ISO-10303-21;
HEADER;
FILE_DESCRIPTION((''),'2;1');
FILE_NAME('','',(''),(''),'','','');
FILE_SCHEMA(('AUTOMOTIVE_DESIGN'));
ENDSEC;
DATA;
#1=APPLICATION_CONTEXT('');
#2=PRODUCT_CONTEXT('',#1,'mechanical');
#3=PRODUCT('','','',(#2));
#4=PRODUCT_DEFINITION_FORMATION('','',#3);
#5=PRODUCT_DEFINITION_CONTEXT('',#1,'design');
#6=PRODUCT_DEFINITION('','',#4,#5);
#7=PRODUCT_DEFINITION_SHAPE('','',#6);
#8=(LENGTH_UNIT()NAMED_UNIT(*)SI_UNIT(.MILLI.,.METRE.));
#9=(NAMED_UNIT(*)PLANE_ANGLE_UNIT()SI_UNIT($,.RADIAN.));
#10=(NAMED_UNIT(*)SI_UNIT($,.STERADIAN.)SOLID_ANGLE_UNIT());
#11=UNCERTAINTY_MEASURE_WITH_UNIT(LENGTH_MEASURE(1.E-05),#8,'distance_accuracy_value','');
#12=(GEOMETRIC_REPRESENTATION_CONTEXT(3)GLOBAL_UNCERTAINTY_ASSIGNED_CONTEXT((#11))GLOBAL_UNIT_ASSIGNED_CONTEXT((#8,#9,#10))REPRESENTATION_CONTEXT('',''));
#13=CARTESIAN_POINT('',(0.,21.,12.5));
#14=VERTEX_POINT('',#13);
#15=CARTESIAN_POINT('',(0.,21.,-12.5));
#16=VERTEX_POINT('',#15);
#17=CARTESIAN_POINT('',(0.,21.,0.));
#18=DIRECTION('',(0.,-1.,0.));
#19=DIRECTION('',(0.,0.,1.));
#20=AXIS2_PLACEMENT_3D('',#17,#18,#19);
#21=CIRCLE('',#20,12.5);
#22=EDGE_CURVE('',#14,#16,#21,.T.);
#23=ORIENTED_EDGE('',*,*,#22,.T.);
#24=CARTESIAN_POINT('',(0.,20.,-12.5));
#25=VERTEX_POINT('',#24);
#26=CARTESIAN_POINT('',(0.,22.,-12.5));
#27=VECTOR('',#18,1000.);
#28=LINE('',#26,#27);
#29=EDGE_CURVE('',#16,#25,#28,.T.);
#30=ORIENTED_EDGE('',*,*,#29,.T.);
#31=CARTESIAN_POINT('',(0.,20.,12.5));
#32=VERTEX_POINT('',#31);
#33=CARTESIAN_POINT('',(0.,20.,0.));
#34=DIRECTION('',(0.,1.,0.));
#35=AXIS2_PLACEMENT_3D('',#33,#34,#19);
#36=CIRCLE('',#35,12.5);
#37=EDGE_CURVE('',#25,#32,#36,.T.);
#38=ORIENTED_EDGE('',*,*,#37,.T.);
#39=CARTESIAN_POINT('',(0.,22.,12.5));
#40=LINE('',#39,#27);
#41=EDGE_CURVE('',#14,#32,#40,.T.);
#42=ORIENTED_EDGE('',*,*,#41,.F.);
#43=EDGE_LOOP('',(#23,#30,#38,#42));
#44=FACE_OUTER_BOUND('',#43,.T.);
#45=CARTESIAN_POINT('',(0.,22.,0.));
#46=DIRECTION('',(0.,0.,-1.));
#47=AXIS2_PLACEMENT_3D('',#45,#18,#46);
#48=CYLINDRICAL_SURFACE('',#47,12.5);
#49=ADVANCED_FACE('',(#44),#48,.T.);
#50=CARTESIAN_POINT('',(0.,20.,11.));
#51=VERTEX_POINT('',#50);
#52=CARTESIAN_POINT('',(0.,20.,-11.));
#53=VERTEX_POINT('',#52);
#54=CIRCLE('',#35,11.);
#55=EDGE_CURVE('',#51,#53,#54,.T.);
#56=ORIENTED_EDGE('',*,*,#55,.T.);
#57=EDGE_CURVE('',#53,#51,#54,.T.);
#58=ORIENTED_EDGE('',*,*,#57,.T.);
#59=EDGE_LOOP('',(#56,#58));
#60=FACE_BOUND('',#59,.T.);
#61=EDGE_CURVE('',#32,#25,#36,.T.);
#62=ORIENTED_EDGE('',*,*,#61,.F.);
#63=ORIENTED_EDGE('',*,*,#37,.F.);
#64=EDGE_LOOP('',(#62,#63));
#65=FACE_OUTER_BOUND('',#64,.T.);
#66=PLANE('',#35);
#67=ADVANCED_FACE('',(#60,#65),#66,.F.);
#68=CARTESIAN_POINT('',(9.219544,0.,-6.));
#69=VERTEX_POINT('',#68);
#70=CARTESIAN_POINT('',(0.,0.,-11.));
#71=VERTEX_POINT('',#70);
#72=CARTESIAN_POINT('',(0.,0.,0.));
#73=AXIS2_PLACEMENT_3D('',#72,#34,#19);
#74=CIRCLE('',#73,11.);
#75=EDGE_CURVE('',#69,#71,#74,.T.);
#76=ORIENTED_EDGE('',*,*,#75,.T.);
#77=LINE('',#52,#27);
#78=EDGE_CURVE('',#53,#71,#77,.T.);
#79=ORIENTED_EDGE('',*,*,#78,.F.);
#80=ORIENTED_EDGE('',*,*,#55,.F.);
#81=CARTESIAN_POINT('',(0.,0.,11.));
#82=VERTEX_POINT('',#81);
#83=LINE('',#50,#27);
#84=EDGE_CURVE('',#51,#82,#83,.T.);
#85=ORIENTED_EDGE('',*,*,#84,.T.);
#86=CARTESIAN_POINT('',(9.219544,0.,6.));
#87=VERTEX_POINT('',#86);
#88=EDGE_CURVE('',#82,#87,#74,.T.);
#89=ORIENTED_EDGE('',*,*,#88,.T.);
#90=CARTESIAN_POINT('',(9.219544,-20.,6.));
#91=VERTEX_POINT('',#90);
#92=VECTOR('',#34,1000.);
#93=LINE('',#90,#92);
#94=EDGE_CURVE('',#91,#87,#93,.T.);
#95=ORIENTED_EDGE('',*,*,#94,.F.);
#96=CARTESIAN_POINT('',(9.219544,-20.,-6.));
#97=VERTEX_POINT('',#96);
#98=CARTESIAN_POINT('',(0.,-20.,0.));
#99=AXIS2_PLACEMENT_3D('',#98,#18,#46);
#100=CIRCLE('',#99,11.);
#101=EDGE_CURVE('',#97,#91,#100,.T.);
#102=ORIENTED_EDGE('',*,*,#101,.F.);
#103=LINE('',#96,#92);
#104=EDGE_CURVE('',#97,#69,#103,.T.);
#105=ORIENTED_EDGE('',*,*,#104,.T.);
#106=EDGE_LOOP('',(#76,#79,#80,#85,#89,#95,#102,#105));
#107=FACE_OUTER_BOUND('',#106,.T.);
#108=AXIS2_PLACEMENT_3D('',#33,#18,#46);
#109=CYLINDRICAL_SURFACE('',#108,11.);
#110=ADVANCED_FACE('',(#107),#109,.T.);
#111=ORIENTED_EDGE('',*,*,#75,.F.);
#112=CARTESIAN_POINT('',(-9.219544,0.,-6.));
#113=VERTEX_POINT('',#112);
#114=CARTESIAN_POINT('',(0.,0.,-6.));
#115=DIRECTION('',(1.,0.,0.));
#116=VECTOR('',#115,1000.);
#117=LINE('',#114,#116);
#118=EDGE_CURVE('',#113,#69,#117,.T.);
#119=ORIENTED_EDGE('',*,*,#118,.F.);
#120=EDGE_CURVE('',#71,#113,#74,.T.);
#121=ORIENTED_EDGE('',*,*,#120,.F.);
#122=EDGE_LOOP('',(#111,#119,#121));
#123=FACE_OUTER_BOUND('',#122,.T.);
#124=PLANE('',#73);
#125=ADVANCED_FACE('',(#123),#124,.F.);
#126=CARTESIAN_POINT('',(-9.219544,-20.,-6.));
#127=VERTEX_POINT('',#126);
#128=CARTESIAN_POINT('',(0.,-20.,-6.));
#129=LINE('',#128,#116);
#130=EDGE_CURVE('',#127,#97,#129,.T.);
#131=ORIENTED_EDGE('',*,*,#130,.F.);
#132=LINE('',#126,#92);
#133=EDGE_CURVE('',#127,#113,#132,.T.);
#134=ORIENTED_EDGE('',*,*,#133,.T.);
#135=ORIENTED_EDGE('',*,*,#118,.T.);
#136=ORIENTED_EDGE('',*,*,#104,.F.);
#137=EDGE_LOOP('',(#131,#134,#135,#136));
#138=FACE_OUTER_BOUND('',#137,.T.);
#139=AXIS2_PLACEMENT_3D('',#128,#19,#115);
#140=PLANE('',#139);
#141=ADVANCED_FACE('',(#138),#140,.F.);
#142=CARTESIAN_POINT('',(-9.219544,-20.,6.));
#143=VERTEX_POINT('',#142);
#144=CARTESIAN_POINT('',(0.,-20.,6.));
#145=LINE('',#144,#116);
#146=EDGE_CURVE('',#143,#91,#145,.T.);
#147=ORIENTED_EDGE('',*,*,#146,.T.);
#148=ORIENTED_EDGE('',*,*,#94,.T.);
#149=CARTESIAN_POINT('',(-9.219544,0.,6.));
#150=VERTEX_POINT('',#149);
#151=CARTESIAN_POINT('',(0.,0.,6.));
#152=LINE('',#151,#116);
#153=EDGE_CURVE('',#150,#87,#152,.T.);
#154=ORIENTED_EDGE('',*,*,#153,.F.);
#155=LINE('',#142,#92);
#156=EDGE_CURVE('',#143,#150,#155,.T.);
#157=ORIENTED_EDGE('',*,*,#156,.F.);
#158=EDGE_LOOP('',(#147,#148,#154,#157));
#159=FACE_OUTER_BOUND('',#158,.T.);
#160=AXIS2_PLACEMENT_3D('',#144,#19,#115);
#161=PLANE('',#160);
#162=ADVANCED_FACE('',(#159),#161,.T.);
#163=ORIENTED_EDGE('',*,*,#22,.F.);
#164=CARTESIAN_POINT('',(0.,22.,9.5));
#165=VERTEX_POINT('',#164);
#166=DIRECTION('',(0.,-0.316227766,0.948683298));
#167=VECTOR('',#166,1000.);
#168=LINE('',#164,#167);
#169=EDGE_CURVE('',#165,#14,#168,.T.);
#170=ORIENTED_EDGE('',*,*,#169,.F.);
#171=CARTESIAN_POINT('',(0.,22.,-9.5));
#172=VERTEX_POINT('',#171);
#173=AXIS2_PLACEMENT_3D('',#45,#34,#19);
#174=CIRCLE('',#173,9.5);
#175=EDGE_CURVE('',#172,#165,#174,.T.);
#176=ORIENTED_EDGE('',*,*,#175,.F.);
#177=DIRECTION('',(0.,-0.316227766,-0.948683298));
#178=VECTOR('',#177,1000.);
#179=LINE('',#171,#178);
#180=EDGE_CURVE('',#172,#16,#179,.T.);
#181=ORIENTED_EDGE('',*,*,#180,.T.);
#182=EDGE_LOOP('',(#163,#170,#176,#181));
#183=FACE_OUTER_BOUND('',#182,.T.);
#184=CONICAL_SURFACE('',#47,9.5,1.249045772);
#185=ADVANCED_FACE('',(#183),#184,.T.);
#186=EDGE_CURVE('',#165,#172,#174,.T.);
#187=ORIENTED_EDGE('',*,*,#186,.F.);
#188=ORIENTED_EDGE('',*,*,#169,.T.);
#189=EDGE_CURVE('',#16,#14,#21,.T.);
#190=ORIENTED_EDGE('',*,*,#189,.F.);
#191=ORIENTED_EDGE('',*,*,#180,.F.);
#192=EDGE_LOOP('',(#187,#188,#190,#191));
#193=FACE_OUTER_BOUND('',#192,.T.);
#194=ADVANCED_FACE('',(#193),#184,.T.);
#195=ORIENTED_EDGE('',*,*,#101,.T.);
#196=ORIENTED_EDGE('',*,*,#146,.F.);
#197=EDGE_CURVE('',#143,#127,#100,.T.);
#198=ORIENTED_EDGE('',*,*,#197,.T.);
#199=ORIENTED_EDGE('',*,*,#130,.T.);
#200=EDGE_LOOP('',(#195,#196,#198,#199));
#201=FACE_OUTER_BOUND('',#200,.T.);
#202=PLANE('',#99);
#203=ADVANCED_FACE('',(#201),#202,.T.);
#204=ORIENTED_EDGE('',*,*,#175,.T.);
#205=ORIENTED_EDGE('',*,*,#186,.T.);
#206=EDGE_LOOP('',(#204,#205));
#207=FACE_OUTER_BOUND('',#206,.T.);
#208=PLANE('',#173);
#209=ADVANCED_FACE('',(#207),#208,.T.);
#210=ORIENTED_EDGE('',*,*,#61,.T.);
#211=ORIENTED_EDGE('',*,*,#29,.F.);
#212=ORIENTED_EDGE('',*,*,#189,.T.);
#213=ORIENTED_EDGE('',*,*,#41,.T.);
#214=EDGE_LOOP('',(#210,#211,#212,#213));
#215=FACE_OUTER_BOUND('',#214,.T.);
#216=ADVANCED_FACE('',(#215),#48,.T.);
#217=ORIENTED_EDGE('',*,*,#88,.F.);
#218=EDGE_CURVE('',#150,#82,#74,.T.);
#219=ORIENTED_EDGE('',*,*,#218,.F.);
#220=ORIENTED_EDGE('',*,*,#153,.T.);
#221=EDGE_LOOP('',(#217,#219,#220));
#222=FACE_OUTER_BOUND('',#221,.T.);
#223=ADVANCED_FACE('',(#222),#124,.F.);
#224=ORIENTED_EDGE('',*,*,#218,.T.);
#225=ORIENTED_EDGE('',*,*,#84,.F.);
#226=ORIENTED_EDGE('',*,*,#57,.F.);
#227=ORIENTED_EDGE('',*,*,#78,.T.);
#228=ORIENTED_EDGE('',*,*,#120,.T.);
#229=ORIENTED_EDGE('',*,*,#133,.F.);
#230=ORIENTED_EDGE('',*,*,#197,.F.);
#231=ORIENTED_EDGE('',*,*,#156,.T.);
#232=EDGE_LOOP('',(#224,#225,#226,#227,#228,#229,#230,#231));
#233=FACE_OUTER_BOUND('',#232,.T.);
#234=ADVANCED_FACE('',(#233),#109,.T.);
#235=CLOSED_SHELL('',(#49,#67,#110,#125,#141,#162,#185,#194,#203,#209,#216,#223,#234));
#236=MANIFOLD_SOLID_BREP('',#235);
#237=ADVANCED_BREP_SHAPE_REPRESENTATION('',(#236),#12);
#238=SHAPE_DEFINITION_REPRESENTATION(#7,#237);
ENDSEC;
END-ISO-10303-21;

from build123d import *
from build123d.topology import SkipClean

# Parameters (mm, degrees)
SKETCH_1_R      = 11
EXTRUDE_1_DEPTH = 20
EXTRUDE_START   = 20
SKETCH_2_W      = 18.439088914
SKETCH_2_H      = 12
EXTRUDE_2_DEPTH = 20
SKETCH_3_R      = 12.5
EXTRUDE_3_DEPTH = 2
CHAMFER_1_SIZE  = 1
CHAMFER_1_SIZE2 = 3


with BuildPart() as part:
    # 草图1 → 凸台-拉伸1 (new body)
    with BuildSketch(Plane(origin=(0, 0, 0), x_dir=(1, 0, 0), z_dir=(0, 1, 0))):
        with Locations(Location((0, 0, 0), (0, 0, 270))):
            Circle(SKETCH_1_R)
    extrude(amount=EXTRUDE_1_DEPTH)

    # 草图2 → 凸台-拉伸2 (add)
    with SkipClean():  # the faces are left unmerged after this step: merging them gives an invalid solid
        with BuildSketch(Plane.XZ.offset(EXTRUDE_START)):
            with BuildLine():
                Line((-9.219544457, -6), (-9.219544457, 6))
                ThreePointArc((-9.219544457, 6), (-11, 0), (-9.219544457, -6))
            make_face()
            Rectangle(SKETCH_2_W, SKETCH_2_H)
            with BuildLine():
                ThreePointArc((11, 0), (10.545496409, 3.129297922), (9.219544457, 6))
                Line((9.219544457, 6), (9.219544457, -6))
                ThreePointArc((9.219544457, -6), (10.545496409, -3.129297922), (11, 0))
            make_face()
        extrude(amount=-EXTRUDE_2_DEPTH)

    # 草图3 → 凸台-拉伸3 (add)
    with SkipClean():  # the faces are left unmerged after this step: merging them gives an invalid solid
        with BuildSketch(Plane(origin=(0, 20, 0), x_dir=(1, 0, 0), z_dir=(0, 1, 0))):
            with Locations(Location((0, 0, 0), (0, 0, 270))):
                Circle(SKETCH_3_R)
        extrude(amount=EXTRUDE_3_DEPTH)

    # 倒角1
    chamfer_1_edges = [part.edges().sort_by_distance(p)[0] for p in [
        (0, 22, -12.5),
    ]]
    chamfer_1_side = [part.faces().sort_by_distance(p)[0] for p in [
        (0, 21, -12.5),
    ]]
    chamfer(chamfer_1_edges, length=CHAMFER_1_SIZE, length2=CHAMFER_1_SIZE2, reference=chamfer_1_side[0])


solid = part.part
